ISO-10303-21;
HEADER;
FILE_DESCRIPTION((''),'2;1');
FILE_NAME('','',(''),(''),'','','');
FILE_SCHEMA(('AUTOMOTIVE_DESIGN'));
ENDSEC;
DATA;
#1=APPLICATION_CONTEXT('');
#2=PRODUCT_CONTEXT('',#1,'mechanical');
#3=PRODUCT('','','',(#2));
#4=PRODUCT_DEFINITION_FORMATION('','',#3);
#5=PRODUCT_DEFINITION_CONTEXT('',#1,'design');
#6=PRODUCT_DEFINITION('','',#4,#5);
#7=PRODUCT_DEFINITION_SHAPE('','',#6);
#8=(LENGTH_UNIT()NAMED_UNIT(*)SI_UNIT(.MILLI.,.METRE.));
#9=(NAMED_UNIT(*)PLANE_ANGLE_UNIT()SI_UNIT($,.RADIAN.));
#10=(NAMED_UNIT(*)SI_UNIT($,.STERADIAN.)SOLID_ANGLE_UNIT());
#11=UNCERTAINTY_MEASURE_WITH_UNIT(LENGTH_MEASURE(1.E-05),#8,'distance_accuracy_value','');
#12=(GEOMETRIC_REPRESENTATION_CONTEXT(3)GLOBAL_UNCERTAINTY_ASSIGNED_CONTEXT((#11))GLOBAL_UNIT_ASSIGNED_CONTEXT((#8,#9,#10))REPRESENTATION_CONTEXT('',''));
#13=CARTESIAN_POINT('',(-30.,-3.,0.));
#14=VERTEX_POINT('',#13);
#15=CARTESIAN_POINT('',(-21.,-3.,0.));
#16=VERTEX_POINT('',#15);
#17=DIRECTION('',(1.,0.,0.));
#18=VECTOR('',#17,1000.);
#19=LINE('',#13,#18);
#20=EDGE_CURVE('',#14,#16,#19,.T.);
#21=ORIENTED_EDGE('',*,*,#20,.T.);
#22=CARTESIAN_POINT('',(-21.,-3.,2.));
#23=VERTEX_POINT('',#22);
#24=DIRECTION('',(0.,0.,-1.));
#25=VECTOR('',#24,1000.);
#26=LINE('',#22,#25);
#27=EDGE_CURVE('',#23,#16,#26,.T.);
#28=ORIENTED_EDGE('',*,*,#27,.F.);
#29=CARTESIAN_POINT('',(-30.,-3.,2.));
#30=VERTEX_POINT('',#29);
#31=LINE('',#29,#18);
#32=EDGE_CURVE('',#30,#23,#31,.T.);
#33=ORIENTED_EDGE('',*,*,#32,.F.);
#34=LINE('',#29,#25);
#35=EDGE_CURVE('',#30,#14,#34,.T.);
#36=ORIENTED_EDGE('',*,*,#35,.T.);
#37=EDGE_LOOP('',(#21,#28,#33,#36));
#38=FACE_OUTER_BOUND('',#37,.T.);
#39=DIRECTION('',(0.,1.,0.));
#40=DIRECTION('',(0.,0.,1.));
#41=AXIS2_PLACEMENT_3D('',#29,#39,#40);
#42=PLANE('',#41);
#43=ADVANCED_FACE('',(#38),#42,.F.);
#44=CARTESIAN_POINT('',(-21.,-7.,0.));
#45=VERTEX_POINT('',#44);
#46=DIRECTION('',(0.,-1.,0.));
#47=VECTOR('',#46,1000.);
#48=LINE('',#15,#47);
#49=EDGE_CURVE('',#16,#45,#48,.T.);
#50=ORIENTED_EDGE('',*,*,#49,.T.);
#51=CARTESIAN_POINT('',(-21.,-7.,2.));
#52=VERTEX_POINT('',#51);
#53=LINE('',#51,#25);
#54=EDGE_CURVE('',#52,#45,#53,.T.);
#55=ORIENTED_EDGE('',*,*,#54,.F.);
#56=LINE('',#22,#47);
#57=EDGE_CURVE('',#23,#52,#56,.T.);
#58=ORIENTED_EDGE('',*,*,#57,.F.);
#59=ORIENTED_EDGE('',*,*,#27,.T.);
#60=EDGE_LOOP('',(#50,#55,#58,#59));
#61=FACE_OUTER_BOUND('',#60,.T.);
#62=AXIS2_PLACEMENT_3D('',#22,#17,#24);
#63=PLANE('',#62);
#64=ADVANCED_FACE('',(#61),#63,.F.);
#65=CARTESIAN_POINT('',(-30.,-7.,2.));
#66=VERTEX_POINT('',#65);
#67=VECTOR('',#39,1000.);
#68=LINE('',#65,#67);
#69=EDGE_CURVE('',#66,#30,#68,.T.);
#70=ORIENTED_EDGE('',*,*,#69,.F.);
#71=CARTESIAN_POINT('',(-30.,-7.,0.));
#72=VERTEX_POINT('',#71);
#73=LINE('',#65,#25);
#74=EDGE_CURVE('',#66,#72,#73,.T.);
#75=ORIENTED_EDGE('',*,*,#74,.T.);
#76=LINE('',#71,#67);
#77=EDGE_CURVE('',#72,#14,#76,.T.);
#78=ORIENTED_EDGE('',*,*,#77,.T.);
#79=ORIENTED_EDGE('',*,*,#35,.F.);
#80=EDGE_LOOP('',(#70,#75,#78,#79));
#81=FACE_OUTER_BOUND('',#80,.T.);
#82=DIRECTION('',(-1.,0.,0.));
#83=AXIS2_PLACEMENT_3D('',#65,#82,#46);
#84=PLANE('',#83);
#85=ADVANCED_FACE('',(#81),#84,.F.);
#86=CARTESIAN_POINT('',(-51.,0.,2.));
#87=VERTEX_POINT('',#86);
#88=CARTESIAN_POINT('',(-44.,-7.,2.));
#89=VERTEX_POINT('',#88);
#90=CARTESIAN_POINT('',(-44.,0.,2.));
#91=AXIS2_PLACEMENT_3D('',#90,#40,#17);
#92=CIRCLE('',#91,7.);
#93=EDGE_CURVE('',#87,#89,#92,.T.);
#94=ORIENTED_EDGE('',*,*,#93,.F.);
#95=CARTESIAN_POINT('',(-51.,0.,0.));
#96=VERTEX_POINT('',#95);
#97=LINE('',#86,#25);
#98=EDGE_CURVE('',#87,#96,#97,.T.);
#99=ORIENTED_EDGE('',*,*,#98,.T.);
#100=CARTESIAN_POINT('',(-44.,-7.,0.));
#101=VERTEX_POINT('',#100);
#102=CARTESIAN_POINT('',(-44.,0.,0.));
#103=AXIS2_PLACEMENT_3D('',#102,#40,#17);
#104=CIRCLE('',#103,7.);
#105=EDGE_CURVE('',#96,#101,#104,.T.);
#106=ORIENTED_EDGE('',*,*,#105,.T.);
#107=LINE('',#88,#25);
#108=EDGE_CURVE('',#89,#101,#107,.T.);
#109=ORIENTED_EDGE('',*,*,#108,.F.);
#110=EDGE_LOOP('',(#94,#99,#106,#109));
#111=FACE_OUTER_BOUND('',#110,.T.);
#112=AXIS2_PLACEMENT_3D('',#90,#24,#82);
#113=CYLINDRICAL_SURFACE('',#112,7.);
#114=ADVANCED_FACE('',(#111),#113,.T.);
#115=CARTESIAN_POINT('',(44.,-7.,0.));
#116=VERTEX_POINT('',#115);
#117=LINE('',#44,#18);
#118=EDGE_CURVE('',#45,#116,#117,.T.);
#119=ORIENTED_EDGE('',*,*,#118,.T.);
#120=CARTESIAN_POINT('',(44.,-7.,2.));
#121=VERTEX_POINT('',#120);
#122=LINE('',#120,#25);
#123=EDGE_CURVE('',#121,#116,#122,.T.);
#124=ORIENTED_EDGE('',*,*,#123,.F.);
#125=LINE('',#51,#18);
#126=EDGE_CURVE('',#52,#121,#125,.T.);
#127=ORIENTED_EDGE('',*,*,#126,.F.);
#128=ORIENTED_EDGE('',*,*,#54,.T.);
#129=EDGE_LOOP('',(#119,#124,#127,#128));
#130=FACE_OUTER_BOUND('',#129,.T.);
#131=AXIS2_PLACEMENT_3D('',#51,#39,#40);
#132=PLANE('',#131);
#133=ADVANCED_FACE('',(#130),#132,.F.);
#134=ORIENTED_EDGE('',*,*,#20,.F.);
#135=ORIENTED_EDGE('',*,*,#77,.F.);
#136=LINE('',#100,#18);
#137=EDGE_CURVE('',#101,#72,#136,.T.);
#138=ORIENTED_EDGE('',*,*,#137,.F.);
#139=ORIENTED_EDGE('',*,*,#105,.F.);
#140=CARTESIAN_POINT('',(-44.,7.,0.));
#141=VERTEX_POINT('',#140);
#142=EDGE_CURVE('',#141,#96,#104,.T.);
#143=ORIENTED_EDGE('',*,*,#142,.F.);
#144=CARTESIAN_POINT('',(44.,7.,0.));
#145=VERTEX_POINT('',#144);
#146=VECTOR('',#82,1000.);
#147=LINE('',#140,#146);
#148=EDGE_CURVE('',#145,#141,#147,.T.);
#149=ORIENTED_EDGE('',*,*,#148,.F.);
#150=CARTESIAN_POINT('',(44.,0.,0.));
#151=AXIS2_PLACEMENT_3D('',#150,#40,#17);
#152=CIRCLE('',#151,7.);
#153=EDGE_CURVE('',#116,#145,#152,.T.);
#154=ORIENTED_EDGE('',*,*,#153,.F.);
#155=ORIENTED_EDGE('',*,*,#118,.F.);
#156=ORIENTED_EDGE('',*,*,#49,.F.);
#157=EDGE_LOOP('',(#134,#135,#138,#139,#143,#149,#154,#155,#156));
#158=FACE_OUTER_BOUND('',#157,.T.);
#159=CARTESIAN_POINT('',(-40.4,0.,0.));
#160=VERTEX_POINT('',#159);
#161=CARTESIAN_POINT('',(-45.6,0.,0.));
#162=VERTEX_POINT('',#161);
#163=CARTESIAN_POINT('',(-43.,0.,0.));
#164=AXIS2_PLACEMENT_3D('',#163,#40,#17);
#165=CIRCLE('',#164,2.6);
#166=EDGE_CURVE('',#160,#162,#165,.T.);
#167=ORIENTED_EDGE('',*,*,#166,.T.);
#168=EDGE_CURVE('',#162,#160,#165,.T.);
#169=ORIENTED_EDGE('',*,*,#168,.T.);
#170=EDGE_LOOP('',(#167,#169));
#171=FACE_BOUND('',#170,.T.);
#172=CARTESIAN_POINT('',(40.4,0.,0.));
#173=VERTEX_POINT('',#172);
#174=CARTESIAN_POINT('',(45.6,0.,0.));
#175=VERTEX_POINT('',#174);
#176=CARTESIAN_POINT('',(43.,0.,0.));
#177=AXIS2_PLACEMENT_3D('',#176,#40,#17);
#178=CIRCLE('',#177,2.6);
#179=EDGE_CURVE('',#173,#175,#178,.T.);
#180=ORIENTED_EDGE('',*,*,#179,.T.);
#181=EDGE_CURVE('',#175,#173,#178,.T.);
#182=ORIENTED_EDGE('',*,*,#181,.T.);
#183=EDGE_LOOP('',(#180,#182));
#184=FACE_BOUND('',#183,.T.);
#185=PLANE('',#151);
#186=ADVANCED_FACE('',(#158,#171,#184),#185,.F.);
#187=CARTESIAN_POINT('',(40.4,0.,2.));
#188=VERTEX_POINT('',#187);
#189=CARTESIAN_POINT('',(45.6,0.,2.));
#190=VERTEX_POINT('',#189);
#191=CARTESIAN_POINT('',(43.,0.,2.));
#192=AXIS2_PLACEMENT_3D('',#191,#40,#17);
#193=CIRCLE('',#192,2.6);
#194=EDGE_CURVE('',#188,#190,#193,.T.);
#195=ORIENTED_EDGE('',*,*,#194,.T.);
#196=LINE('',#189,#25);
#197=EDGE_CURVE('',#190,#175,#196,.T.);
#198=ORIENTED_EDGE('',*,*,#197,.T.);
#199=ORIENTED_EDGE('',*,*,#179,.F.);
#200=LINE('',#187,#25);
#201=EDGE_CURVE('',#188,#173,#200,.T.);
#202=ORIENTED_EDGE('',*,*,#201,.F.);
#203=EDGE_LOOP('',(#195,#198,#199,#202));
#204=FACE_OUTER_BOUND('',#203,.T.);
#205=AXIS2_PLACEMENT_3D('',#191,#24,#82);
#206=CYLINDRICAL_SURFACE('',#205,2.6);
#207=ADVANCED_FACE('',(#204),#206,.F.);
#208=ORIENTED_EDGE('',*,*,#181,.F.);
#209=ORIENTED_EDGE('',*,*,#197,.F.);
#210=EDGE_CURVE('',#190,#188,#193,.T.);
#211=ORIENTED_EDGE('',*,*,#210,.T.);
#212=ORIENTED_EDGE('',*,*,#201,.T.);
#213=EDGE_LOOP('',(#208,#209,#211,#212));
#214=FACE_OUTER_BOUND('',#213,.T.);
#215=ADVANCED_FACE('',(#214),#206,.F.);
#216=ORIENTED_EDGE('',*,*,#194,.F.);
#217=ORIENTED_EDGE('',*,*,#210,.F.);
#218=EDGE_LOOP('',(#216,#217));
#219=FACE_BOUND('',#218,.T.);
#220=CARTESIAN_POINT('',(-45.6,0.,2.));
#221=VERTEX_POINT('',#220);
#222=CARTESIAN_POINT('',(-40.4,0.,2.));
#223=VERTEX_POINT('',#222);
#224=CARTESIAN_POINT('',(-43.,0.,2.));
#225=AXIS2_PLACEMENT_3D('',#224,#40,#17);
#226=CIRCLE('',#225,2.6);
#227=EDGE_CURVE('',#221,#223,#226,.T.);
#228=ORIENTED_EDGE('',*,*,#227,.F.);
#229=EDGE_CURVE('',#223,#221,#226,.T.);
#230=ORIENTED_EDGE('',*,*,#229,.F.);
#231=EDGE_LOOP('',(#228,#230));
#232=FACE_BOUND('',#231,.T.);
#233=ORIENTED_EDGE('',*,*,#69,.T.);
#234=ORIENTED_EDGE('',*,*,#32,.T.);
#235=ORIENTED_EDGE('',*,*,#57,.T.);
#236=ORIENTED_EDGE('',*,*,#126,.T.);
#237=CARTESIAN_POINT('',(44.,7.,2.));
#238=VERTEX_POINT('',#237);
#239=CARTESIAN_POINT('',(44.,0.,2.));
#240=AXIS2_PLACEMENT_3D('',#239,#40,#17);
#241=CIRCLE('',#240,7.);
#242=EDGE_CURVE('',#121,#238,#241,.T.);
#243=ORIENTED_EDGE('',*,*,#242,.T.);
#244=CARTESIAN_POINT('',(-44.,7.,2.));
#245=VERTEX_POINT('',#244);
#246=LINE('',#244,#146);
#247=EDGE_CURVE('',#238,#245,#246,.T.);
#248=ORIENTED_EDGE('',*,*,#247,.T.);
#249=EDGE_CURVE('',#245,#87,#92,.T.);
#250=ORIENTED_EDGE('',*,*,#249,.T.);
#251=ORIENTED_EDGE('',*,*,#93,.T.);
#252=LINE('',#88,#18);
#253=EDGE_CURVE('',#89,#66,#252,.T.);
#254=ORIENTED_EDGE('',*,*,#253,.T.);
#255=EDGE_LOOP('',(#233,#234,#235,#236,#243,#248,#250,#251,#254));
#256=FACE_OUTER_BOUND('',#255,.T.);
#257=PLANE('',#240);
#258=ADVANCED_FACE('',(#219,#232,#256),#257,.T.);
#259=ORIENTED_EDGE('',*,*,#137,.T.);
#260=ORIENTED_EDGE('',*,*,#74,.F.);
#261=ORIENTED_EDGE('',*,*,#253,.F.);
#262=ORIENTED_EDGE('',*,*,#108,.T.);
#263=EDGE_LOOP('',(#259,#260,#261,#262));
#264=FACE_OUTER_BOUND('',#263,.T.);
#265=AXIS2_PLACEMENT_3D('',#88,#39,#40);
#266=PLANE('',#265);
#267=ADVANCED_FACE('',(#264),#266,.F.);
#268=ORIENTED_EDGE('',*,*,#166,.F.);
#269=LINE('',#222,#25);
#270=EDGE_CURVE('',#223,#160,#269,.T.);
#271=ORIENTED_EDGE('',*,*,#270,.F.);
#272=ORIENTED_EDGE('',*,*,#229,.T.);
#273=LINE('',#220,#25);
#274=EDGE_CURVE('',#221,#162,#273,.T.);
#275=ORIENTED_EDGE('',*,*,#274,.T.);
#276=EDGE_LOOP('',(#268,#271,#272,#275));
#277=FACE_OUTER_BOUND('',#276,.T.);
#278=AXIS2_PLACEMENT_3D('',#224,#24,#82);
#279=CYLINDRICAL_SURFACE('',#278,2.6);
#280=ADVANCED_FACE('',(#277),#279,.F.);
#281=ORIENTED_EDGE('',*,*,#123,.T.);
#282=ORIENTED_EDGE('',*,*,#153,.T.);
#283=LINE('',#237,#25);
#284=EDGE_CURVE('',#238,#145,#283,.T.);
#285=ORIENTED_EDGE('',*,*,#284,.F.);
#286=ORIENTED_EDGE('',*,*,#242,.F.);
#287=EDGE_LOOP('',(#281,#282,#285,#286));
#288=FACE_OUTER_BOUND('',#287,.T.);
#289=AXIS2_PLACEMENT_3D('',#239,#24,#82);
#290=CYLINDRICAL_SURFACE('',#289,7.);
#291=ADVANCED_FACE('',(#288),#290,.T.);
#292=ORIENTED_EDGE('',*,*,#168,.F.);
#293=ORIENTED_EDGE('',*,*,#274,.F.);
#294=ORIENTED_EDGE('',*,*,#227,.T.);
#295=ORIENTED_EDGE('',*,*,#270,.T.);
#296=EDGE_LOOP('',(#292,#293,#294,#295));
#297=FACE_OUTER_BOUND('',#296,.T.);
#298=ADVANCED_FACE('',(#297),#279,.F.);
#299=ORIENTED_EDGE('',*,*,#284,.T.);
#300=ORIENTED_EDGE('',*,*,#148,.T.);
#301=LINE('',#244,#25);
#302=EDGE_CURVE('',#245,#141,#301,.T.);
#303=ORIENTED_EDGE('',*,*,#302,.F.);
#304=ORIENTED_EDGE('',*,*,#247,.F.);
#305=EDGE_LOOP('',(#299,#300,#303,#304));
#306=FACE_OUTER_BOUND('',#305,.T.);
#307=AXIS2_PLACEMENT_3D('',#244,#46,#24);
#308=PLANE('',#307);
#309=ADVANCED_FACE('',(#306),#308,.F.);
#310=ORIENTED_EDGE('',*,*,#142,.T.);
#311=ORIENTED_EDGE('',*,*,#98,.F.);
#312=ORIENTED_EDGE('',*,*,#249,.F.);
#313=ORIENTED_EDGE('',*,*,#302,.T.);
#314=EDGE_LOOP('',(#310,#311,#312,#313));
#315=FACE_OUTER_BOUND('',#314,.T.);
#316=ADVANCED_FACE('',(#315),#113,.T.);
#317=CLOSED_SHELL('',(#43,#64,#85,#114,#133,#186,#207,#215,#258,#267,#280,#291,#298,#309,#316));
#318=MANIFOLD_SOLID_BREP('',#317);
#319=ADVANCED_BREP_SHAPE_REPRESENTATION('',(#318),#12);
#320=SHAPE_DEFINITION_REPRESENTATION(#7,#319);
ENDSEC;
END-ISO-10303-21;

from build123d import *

# Parameters (mm, degrees)
SKETCH1_R      = 2.6
EXTRUDE1_DEPTH = 2


with BuildPart() as part:
    # Sketch1 → Extrude1 (new body)
    with BuildSketch(Plane.XY):
        with BuildLine():
            Line((-30, -7), (-30, -3))
            Line((-30, -3), (-21, -3))
            Line((-21, -3), (-21, -7))
            Line((-21, -7), (44, -7))
            ThreePointArc((44, -7), (51, 0), (44, 7))
            Line((44, 7), (-44, 7))
            ThreePointArc((-44, 7), (-51, 0), (-44, -7))
            Line((-44, -7), (-30, -7))
        make_face()
        with Locations(Location((-43, 0, 0), (0, 0, 180))):
            Circle(SKETCH1_R, mode=Mode.SUBTRACT)
        with Locations(Location((43, 0, 0), (0, 0, 180))):
            Circle(SKETCH1_R, mode=Mode.SUBTRACT)
    extrude(amount=EXTRUDE1_DEPTH)


solid = part.part
